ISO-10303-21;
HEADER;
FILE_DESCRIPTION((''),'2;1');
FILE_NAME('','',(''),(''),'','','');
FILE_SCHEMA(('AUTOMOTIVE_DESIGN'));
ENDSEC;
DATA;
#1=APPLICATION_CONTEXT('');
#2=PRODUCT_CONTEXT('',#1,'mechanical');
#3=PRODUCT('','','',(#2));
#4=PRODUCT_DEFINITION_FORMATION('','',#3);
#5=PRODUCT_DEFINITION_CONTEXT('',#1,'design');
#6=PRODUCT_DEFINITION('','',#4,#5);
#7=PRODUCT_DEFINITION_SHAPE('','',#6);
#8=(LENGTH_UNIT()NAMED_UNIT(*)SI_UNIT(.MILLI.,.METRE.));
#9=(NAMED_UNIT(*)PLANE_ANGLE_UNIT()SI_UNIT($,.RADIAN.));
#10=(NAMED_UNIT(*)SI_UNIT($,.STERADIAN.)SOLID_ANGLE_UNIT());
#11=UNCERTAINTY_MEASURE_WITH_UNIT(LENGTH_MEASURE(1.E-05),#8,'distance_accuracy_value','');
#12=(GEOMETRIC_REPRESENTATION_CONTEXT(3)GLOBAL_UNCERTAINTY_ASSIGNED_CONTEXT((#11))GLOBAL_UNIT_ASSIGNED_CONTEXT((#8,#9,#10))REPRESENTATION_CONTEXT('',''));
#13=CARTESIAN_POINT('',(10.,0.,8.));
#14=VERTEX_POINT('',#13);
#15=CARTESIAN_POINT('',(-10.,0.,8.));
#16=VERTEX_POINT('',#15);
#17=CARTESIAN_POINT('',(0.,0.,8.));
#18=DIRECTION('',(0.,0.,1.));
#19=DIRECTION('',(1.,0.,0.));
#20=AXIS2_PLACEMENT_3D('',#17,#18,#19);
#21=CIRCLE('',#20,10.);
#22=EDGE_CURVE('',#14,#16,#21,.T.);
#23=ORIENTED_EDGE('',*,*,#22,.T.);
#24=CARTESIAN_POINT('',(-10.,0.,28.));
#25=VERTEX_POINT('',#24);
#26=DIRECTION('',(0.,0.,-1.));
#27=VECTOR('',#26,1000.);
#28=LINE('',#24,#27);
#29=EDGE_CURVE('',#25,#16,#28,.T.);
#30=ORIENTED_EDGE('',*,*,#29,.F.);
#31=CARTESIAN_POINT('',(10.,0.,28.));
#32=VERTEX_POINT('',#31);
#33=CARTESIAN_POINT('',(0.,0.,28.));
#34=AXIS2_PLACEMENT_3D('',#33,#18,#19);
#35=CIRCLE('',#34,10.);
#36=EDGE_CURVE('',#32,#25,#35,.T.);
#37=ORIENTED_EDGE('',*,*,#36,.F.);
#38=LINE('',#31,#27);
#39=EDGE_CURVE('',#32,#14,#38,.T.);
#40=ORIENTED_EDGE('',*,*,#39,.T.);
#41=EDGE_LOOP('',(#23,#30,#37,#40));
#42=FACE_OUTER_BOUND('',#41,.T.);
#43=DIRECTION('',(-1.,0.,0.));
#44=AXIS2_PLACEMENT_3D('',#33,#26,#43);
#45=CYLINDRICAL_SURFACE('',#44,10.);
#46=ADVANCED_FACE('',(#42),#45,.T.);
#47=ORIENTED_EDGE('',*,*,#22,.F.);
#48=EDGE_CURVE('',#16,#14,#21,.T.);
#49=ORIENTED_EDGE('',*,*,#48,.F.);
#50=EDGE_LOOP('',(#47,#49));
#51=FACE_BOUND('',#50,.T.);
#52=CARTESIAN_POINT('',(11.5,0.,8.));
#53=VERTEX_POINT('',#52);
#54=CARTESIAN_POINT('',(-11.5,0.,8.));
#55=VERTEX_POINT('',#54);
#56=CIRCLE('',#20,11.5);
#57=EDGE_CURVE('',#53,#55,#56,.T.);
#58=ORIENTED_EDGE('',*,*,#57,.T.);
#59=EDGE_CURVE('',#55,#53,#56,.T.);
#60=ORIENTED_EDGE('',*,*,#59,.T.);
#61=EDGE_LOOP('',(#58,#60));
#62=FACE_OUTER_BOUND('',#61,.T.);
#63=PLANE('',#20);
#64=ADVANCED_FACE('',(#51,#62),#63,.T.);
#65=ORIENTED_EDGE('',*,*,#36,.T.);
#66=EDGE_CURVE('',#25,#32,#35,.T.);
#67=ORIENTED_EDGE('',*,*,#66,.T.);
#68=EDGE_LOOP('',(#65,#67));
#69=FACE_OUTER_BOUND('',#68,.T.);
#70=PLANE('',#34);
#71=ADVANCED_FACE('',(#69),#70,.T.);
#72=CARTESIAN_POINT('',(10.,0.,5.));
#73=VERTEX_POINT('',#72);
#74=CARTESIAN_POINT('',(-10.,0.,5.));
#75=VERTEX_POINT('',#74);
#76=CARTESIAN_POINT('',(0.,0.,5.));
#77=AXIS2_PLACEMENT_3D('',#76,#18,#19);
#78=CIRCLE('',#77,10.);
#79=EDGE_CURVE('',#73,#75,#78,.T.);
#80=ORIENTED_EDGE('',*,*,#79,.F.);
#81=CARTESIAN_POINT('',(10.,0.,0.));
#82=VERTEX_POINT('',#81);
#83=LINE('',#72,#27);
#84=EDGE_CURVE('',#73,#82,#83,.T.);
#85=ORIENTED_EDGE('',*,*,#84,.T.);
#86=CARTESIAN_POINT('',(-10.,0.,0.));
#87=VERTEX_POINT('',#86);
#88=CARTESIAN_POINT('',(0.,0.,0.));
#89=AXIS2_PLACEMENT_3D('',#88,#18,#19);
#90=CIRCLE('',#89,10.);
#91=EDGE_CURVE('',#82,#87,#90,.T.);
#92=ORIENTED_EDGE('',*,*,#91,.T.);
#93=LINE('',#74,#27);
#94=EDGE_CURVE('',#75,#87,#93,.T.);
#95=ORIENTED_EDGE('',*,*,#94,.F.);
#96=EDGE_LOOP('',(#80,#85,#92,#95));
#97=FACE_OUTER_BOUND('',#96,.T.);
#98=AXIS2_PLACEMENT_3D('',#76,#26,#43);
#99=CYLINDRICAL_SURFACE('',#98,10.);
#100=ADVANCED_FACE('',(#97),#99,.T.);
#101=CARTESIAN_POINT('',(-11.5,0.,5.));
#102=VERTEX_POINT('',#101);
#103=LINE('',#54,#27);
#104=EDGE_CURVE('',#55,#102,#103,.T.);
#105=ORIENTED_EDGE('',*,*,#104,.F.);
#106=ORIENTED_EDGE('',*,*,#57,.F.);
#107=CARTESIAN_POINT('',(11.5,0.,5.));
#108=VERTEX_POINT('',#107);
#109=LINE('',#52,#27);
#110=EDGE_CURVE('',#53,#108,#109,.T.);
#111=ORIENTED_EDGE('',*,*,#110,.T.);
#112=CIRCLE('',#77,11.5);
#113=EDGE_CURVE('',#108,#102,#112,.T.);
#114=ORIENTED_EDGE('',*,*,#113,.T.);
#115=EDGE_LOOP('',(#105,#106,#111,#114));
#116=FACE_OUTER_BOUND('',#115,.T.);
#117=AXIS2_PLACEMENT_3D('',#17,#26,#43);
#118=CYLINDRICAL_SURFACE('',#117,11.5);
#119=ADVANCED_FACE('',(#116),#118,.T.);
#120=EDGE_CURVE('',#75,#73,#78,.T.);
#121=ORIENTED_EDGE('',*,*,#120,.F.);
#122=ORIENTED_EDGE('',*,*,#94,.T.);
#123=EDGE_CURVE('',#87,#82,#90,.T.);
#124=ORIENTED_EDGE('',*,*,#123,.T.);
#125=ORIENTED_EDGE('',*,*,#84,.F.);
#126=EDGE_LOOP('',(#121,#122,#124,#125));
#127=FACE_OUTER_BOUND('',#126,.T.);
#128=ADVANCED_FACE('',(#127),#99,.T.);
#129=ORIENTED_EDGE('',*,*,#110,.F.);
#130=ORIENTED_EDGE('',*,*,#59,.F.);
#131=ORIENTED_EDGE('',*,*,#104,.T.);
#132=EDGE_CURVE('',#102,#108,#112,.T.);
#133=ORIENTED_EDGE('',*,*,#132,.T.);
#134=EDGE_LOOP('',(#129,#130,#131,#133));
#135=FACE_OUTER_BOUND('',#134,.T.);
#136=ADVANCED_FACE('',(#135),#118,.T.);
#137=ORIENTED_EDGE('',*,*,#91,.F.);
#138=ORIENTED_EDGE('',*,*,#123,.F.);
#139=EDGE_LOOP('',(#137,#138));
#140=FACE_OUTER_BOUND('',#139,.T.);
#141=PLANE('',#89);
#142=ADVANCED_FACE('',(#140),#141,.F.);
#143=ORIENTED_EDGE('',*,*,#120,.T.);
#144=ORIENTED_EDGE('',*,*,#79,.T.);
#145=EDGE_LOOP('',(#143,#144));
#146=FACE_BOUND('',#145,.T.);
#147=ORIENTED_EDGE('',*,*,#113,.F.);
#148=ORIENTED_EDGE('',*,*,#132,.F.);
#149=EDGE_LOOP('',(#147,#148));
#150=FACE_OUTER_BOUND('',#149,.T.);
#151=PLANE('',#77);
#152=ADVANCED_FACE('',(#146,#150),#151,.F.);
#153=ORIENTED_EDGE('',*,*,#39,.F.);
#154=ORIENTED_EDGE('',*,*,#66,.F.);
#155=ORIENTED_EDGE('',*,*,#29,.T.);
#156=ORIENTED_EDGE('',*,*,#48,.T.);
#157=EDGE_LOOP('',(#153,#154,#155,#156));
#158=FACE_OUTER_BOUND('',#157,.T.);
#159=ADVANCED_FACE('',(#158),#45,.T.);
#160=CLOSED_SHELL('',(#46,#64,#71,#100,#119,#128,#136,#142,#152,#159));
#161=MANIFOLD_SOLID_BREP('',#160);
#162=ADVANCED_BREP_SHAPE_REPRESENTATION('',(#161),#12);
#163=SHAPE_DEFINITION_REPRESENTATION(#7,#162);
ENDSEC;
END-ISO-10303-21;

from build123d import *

# Parameters (mm, degrees)
SKETCH1_R           = 10
BOSS_EXTRUDE2_DEPTH = 5
SKETCH2_R           = 11.5
BOSS_EXTRUDE3_DEPTH = 3
SKETCH3_R           = 10
BOSS_EXTRUDE4_DEPTH = 20


with BuildPart() as part:
    # Sketch1 → Boss-Extrude2 (new body)
    with BuildSketch(Plane.XY):
        Circle(SKETCH1_R)
    extrude(amount=BOSS_EXTRUDE2_DEPTH)

    # Sketch2 → Boss-Extrude3 (add)
    with BuildSketch(Plane.XY.offset(5)):
        Circle(SKETCH2_R)
    extrude(amount=BOSS_EXTRUDE3_DEPTH)

    # Sketch3 → Boss-Extrude4 (add)
    with BuildSketch(Plane.XY.offset(8)):
        Circle(SKETCH3_R)
    extrude(amount=BOSS_EXTRUDE4_DEPTH)


solid = part.part
